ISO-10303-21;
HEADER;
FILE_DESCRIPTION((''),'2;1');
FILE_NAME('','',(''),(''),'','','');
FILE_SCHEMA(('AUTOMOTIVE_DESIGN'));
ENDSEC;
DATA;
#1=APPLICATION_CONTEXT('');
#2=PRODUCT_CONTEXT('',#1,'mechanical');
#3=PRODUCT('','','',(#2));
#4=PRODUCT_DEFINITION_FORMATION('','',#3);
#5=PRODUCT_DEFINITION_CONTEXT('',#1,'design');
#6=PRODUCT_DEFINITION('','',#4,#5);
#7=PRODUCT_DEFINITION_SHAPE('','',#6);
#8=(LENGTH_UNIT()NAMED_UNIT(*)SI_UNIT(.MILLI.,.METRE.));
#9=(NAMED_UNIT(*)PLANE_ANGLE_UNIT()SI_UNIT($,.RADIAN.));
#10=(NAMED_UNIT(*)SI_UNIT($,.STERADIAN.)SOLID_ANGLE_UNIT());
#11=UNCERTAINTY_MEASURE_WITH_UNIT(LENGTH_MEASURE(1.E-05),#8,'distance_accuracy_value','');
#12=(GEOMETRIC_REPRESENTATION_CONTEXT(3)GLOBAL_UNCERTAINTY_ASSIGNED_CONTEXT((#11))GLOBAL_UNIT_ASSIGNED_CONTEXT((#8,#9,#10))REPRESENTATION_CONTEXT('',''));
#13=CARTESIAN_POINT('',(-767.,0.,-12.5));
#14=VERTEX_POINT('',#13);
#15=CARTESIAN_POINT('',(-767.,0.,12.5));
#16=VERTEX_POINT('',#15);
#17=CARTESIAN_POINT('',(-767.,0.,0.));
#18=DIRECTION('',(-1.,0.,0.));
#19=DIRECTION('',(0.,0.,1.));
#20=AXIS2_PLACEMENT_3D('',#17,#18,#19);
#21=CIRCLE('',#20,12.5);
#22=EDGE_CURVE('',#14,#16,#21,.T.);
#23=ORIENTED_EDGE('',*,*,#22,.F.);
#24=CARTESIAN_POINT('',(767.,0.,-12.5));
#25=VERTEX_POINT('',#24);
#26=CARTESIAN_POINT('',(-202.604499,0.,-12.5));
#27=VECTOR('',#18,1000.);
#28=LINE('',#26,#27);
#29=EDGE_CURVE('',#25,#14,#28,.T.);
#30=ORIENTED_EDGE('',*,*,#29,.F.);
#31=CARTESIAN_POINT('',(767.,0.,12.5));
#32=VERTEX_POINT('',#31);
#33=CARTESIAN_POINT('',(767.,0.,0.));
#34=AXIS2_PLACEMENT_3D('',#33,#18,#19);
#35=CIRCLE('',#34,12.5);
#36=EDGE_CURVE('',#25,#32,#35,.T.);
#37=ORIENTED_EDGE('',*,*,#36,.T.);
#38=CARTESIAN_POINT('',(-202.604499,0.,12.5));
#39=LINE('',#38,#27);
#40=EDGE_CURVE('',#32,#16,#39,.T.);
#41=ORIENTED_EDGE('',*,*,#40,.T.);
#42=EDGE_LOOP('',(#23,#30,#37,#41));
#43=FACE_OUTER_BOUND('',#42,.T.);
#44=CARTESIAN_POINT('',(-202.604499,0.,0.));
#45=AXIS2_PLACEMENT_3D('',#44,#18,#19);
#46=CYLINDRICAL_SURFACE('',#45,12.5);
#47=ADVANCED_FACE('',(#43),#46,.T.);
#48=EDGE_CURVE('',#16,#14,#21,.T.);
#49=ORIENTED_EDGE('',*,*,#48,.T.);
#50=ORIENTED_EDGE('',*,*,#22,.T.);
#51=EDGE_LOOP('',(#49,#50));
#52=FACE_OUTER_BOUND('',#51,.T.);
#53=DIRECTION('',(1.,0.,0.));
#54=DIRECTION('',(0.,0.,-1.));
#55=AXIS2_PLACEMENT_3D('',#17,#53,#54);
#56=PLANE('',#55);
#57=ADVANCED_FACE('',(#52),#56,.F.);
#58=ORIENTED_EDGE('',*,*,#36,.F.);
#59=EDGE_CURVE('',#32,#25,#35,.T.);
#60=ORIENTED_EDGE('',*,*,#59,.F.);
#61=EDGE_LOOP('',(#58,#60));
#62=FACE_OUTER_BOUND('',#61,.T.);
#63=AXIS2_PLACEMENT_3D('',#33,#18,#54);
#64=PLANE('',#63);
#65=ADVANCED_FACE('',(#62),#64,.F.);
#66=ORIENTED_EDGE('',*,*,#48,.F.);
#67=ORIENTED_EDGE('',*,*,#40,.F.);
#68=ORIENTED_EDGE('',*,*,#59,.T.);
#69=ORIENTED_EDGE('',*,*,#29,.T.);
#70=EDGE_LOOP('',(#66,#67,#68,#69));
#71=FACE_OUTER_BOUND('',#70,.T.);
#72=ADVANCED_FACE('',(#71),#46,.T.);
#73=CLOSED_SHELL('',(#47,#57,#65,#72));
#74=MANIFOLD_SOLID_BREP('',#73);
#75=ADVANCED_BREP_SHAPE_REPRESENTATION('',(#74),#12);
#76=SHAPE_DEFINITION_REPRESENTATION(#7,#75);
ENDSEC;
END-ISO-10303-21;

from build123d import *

# Parameters (mm, degrees)
SKETCH1_W = 767
SKETCH1_H = 12.5


with BuildPart() as part:
    # Sketch1 → Revolve1 (revolve)
    with BuildSketch(Plane.XY, mode=Mode.PRIVATE) as revolve1_sk:
        with Locations((-383.5, 6.25)):
            Rectangle(SKETCH1_W, SKETCH1_H)
    revolve1 = revolve(revolve1_sk.sketch.rotate(Axis((-202.604499093, 0, 0), (1, 0, 0)), 90), axis=Axis((-202.604499093, 0, 0), (1, 0, 0)))

    # Mirror1: Revolve1 across plane
    add(revolve1.mirror(Plane(origin=(0, 0, 0), x_dir=(0, 0, 1), z_dir=(1, 0, 0))))


solid = part.part
